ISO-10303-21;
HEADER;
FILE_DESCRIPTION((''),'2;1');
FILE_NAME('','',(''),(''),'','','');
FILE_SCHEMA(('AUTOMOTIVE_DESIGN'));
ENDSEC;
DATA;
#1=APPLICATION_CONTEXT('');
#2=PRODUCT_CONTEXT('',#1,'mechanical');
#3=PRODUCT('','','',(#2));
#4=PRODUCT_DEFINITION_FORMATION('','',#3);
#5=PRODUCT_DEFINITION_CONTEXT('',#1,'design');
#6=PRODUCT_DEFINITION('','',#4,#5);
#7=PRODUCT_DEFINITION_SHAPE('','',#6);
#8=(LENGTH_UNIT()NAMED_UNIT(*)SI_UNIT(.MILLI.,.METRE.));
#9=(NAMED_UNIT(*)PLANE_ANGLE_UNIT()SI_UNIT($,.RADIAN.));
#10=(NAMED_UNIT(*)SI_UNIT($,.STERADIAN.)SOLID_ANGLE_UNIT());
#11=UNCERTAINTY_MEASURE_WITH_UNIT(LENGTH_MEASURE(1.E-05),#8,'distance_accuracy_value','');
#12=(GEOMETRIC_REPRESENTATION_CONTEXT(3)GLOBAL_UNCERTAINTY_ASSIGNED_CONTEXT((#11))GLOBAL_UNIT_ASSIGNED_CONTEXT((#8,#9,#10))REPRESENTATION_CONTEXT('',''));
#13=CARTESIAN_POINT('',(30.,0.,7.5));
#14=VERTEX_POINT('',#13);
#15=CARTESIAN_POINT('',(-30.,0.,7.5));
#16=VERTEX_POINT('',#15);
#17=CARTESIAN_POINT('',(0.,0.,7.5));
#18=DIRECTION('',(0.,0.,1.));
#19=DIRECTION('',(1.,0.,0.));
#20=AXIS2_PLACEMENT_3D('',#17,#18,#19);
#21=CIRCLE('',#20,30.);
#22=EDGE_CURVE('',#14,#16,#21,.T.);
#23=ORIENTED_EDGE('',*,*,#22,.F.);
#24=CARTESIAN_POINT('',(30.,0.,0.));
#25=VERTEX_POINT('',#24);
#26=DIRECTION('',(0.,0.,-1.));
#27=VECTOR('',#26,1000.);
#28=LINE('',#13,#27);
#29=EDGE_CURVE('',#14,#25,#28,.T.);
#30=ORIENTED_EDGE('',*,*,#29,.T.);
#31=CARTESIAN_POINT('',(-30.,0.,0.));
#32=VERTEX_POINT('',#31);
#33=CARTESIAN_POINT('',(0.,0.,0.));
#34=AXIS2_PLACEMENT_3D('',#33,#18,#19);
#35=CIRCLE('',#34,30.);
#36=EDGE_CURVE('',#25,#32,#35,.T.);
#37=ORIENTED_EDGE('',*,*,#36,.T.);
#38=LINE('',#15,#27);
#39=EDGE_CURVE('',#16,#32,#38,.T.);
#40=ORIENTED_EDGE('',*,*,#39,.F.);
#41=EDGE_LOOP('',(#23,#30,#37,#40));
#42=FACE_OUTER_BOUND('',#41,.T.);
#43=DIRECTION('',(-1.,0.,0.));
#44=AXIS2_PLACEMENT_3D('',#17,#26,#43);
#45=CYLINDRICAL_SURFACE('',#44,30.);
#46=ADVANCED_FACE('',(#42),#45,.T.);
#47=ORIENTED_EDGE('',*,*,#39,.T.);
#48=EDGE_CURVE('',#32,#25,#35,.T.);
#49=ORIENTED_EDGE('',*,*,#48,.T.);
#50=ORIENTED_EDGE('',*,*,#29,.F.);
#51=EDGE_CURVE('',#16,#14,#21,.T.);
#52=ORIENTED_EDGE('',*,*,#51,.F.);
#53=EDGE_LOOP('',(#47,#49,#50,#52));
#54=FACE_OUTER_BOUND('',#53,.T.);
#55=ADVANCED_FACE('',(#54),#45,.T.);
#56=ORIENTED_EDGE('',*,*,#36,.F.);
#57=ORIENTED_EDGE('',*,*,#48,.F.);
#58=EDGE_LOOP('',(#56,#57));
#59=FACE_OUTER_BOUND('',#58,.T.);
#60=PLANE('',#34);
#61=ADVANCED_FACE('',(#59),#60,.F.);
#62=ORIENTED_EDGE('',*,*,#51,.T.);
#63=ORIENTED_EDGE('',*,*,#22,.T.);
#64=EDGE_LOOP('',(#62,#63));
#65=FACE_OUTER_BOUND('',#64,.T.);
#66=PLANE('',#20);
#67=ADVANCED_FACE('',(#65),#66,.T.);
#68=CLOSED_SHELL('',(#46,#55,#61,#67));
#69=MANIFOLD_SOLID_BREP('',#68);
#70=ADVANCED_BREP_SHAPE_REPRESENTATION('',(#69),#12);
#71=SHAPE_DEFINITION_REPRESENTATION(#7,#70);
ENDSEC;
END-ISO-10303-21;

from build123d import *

# Parameters (mm, degrees)
SKETCH1_R           = 30
BOSS_EXTRUDE1_DEPTH = 7.5


with BuildPart() as part:
    # Sketch1 → Boss-Extrude1 (new body)
    with BuildSketch(Plane.XY):
        Circle(SKETCH1_R)
    extrude(amount=BOSS_EXTRUDE1_DEPTH)


solid = part.part
